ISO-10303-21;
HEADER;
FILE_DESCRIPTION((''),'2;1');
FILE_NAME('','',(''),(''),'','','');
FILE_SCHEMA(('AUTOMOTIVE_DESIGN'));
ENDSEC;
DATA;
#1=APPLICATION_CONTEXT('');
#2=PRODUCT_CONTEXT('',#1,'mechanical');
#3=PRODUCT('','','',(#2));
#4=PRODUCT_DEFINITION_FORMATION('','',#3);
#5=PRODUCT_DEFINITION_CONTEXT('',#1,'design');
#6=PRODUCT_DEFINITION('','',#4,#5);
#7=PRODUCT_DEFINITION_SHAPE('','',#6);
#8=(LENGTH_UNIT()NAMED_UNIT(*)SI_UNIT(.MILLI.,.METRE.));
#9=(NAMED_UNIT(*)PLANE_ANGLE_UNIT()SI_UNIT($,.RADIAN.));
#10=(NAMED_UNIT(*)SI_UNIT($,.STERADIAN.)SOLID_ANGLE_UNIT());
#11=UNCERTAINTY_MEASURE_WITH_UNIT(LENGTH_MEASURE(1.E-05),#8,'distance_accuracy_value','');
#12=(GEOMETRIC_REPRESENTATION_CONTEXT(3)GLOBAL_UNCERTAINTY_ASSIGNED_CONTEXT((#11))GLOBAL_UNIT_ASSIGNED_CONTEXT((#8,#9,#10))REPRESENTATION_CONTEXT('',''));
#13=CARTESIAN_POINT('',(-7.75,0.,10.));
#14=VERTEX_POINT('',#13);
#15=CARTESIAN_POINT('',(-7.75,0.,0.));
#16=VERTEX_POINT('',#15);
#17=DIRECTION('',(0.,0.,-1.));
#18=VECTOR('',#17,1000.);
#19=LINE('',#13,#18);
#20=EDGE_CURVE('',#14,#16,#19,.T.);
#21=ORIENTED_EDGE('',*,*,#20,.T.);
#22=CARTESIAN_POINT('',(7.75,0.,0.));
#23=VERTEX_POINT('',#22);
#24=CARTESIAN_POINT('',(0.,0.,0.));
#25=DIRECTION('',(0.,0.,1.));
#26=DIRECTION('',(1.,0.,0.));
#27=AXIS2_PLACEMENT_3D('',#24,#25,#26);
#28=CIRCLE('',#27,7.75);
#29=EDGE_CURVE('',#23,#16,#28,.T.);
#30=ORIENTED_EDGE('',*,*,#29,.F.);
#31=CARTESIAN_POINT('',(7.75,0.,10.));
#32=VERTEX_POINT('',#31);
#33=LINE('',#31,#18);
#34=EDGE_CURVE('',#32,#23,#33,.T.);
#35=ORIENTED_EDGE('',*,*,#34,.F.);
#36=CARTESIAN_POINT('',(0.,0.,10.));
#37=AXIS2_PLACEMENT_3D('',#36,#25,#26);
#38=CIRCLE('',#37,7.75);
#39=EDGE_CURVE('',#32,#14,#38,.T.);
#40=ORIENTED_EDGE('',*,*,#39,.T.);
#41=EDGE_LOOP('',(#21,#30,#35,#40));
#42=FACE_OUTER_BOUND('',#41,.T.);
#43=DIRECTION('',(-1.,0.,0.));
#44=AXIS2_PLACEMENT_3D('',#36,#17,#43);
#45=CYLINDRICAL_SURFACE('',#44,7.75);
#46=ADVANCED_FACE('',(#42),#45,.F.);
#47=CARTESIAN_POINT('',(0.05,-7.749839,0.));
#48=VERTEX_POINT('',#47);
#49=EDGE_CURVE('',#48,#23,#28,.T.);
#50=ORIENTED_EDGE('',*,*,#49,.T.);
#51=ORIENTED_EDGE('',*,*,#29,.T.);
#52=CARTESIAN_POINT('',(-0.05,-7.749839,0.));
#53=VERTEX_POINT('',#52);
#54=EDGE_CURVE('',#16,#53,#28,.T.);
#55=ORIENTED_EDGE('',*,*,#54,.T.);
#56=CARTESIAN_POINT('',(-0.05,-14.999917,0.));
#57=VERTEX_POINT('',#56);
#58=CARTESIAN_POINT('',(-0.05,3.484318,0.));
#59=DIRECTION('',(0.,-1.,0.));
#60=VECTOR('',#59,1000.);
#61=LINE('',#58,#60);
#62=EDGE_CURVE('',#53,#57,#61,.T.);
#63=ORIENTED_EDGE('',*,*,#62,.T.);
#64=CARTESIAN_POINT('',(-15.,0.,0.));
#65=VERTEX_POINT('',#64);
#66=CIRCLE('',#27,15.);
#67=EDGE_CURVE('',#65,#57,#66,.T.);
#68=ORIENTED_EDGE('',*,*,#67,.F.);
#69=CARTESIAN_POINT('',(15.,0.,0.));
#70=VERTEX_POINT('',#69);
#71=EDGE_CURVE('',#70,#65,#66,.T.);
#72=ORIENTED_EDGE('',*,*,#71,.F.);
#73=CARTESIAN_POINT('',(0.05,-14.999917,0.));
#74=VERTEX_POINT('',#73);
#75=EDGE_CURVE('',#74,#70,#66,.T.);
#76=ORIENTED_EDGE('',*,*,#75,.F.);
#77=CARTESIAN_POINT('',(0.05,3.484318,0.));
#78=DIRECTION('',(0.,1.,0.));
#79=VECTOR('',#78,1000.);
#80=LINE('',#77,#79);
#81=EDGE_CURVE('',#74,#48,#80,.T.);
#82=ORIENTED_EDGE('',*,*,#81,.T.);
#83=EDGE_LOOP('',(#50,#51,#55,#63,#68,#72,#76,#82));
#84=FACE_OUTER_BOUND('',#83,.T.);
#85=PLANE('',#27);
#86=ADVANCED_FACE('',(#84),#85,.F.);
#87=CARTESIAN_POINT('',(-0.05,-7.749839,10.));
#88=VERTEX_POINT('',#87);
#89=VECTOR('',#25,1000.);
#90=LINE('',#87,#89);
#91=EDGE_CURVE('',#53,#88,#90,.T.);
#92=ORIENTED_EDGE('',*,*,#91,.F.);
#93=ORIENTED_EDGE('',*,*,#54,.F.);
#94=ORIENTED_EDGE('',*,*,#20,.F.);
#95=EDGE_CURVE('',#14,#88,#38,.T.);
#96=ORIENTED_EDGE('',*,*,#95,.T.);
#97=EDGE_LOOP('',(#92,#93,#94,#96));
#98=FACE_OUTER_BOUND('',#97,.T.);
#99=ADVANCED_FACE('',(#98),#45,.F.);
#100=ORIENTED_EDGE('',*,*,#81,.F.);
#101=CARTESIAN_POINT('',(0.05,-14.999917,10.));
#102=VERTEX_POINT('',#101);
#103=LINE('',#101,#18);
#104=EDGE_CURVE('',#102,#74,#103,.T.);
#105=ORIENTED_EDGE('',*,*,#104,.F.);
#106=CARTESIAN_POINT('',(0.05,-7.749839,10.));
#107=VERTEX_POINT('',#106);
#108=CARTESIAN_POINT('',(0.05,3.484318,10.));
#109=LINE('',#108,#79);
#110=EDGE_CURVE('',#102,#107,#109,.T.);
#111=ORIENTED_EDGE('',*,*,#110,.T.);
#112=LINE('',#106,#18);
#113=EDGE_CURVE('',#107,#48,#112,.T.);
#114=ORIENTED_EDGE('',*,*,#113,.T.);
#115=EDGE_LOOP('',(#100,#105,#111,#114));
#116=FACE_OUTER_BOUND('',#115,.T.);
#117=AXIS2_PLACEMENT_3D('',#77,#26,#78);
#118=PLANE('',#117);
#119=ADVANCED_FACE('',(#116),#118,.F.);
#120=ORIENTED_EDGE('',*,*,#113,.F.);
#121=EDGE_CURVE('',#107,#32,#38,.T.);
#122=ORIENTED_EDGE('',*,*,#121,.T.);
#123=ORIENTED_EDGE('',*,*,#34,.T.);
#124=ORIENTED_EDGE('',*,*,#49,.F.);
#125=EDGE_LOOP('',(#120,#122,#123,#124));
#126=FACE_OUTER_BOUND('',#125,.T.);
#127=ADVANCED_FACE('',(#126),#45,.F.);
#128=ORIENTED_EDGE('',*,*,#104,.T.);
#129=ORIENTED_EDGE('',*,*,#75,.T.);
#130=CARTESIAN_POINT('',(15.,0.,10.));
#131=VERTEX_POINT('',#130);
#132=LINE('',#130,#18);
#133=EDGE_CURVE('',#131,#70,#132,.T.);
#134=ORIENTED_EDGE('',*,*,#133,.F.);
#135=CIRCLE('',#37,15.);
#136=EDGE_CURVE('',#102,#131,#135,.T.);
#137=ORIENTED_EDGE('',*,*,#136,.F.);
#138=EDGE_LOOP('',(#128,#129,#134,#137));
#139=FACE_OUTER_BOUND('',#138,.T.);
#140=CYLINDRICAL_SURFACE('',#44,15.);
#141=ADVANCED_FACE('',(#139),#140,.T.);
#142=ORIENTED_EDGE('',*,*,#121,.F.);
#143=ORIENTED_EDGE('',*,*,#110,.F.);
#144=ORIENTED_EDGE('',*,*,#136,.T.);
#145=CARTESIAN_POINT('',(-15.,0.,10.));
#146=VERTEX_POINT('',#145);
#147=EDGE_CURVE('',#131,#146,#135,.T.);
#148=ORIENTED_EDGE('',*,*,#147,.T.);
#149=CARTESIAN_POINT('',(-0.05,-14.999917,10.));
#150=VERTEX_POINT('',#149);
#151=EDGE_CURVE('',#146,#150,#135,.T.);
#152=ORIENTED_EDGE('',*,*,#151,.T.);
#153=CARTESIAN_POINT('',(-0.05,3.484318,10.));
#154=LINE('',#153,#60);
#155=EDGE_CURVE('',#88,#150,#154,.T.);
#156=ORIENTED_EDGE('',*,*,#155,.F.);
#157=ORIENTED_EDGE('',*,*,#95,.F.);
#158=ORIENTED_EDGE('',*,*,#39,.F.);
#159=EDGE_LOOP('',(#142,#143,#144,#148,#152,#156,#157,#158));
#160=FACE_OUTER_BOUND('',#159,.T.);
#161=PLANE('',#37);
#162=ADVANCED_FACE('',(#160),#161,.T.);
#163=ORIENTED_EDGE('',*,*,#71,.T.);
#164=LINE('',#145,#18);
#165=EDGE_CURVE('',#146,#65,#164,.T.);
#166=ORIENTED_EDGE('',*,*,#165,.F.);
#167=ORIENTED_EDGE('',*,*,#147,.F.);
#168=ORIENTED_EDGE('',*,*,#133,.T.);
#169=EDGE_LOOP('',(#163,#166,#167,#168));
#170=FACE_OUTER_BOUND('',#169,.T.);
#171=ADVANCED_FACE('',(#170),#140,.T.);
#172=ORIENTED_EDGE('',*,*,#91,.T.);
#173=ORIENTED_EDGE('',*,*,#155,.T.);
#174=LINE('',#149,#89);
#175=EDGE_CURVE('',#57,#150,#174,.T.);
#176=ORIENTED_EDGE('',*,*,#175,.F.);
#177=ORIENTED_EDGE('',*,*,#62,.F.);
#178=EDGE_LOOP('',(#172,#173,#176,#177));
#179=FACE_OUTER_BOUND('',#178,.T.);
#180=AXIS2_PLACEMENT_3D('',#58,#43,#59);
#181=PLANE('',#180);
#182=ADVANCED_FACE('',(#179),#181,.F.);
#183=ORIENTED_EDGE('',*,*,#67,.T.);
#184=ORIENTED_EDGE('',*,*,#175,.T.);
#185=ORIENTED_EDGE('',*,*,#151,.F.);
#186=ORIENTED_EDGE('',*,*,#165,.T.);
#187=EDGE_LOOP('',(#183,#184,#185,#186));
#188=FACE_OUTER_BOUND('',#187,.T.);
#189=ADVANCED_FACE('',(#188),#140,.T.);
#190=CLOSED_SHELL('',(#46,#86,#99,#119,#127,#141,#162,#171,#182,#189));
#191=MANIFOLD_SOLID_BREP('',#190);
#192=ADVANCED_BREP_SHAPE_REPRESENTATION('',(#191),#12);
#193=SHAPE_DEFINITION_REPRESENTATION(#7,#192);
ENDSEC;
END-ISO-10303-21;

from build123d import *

# Parameters (mm, degrees)
SKETCH1_R           = 15
SKETCH1_R_2         = 7.75
BOSS_EXTRUDE1_DEPTH = 10
SKETCH2_W           = 0.1
SKETCH2_H           = 22.468635184
CUT_EXTRUDE1_DEPTH  = 24.452078799


with BuildPart() as part:
    # Sketch1 → Boss-Extrude1 (new body)
    with BuildSketch(Plane.XY):
        Circle(SKETCH1_R)
        Circle(SKETCH1_R_2, mode=Mode.SUBTRACT)
    extrude(amount=BOSS_EXTRUDE1_DEPTH)

    # Sketch2 → Cut-Extrude1 (cut, through all)
    with BuildSketch(Plane.XY.offset(10)):
        with Locations((0, -7.75)):
            Rectangle(SKETCH2_W, SKETCH2_H)
    extrude(amount=-CUT_EXTRUDE1_DEPTH, mode=Mode.SUBTRACT)


solid = part.part
